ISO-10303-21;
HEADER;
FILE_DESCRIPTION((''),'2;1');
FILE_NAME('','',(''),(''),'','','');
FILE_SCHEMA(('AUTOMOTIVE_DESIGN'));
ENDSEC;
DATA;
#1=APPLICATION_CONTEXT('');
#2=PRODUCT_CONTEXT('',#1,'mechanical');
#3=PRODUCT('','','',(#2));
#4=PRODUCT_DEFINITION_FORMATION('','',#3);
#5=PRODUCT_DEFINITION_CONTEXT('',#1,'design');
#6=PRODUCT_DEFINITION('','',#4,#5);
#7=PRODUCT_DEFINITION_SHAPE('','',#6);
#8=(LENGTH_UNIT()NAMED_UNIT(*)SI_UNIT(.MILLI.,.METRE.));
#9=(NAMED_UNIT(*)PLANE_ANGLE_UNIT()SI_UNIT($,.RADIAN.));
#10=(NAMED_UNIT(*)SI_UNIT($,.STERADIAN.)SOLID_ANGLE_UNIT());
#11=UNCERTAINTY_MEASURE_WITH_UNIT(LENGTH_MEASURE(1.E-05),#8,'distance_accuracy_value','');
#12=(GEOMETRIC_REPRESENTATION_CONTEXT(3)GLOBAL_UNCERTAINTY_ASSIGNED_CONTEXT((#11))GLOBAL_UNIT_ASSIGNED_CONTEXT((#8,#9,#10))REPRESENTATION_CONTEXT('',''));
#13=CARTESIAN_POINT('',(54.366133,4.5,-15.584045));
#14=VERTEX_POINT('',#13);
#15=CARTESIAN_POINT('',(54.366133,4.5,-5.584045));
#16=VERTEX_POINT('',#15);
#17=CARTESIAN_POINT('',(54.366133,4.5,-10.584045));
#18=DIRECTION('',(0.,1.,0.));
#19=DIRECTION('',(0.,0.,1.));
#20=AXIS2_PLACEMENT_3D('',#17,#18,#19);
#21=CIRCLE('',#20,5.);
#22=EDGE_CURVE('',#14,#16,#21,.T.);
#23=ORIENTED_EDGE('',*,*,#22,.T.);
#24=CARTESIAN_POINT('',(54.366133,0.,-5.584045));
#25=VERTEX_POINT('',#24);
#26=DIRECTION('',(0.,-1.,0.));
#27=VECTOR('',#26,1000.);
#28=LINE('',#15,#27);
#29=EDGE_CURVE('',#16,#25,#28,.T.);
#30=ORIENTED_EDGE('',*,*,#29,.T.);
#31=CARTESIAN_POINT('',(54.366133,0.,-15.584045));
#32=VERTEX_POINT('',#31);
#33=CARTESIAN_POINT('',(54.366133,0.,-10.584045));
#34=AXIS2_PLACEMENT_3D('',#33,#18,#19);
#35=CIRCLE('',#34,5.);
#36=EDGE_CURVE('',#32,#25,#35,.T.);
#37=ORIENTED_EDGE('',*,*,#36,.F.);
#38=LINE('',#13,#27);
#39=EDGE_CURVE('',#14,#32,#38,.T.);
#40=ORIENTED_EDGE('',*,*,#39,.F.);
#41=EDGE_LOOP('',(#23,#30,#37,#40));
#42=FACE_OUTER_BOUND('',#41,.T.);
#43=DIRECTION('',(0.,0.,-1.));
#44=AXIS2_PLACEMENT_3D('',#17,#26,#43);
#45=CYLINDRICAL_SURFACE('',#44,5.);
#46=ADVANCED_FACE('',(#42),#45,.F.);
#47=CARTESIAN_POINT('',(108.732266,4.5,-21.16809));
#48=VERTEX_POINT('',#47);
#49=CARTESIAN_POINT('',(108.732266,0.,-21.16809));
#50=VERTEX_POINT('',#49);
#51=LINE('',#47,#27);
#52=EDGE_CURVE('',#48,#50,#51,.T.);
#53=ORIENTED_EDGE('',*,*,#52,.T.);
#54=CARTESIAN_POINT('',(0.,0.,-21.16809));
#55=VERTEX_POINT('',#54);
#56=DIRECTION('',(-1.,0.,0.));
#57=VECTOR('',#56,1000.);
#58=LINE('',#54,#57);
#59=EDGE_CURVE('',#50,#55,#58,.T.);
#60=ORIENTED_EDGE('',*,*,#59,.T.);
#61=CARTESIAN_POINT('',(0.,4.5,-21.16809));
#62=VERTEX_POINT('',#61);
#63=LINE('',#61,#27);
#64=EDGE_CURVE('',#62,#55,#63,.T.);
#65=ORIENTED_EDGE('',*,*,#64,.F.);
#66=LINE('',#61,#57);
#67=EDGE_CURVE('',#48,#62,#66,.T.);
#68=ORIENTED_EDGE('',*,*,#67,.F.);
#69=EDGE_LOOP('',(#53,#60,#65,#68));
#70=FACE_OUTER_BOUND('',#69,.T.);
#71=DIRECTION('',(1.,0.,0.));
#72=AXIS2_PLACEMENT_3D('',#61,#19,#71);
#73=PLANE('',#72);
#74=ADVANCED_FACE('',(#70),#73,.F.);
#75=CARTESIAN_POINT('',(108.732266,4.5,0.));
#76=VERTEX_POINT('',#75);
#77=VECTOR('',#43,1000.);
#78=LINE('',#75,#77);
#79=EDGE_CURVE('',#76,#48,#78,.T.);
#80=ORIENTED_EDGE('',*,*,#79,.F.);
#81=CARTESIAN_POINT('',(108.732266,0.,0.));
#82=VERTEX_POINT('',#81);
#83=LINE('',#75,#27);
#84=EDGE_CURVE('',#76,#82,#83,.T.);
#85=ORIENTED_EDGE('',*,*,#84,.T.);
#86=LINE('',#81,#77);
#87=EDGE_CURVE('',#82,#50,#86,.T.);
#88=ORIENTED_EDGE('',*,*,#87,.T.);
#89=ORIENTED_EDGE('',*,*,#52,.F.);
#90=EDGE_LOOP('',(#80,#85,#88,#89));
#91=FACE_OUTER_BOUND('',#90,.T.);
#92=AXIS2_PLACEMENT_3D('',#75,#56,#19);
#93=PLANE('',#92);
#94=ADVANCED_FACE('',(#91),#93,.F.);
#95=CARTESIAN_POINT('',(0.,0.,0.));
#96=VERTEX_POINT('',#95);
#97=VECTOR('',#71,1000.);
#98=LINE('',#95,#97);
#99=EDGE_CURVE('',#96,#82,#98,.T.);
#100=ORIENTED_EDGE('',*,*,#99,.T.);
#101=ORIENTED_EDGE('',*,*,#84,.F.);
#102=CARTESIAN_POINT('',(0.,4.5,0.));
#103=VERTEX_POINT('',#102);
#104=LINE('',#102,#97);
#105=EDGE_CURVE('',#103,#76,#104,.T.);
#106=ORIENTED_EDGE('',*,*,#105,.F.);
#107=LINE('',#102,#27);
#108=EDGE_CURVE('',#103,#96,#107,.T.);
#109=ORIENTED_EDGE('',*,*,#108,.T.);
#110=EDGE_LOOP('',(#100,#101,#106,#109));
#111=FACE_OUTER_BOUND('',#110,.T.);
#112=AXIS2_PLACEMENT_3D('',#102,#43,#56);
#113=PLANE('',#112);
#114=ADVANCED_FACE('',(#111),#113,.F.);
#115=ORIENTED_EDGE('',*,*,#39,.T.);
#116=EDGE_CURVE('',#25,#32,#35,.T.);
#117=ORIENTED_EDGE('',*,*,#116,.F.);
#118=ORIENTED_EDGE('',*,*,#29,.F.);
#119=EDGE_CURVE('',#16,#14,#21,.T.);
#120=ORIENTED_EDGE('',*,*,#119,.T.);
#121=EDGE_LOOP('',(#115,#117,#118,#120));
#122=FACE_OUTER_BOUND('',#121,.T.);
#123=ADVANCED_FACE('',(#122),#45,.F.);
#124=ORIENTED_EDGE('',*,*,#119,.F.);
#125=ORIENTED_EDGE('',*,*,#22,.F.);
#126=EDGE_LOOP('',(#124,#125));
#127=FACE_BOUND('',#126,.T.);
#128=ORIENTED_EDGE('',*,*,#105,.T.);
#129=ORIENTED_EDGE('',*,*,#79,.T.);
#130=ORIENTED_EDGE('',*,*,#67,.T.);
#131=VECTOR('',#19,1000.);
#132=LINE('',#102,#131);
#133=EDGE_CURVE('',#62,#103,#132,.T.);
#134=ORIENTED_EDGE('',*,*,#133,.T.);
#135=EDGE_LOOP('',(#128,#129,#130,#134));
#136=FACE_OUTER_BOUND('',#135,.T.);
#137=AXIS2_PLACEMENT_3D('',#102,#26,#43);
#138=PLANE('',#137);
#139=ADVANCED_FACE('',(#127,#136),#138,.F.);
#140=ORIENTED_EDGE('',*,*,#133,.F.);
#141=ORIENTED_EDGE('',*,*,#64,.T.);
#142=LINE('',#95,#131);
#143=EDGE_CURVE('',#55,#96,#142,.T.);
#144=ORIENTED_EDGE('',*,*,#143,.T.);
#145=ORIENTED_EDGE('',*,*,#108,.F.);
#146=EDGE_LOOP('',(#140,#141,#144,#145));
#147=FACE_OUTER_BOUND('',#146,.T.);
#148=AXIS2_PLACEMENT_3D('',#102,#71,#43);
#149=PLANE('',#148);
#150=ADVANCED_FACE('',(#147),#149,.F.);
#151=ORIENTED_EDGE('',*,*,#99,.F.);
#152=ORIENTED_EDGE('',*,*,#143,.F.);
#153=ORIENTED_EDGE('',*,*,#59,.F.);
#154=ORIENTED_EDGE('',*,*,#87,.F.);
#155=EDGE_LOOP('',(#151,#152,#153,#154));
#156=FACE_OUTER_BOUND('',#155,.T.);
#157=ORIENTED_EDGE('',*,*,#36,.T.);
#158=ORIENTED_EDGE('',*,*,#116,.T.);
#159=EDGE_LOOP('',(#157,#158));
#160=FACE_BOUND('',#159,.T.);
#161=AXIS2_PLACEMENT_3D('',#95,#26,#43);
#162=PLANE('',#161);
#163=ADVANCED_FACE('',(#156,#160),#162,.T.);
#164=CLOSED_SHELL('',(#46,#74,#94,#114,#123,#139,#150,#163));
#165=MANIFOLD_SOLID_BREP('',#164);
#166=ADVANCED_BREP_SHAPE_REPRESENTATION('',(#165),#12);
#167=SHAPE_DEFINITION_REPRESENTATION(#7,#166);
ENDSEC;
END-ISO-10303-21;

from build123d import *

# Parameters (mm, degrees)
SKETCH1_W           = 108.732266051
SKETCH1_H           = 21.168090093
SKETCH1_R           = 5
BOSS_EXTRUDE1_DEPTH = 4.5


with BuildPart() as part:
    # Sketch1 → Boss-Extrude1 (new body)
    with BuildSketch(Plane(origin=(0, 0, 0), x_dir=(1, 0, 0), z_dir=(0, 1, 0))):
        with Locations((54.366133026, 10.584045046)):
            Rectangle(SKETCH1_W, SKETCH1_H)
        with Locations(Location((54.366133025, 10.584045046, 0), (0, 0, 270))):
            Circle(SKETCH1_R, mode=Mode.SUBTRACT)
    extrude(amount=BOSS_EXTRUDE1_DEPTH)


solid = part.part
